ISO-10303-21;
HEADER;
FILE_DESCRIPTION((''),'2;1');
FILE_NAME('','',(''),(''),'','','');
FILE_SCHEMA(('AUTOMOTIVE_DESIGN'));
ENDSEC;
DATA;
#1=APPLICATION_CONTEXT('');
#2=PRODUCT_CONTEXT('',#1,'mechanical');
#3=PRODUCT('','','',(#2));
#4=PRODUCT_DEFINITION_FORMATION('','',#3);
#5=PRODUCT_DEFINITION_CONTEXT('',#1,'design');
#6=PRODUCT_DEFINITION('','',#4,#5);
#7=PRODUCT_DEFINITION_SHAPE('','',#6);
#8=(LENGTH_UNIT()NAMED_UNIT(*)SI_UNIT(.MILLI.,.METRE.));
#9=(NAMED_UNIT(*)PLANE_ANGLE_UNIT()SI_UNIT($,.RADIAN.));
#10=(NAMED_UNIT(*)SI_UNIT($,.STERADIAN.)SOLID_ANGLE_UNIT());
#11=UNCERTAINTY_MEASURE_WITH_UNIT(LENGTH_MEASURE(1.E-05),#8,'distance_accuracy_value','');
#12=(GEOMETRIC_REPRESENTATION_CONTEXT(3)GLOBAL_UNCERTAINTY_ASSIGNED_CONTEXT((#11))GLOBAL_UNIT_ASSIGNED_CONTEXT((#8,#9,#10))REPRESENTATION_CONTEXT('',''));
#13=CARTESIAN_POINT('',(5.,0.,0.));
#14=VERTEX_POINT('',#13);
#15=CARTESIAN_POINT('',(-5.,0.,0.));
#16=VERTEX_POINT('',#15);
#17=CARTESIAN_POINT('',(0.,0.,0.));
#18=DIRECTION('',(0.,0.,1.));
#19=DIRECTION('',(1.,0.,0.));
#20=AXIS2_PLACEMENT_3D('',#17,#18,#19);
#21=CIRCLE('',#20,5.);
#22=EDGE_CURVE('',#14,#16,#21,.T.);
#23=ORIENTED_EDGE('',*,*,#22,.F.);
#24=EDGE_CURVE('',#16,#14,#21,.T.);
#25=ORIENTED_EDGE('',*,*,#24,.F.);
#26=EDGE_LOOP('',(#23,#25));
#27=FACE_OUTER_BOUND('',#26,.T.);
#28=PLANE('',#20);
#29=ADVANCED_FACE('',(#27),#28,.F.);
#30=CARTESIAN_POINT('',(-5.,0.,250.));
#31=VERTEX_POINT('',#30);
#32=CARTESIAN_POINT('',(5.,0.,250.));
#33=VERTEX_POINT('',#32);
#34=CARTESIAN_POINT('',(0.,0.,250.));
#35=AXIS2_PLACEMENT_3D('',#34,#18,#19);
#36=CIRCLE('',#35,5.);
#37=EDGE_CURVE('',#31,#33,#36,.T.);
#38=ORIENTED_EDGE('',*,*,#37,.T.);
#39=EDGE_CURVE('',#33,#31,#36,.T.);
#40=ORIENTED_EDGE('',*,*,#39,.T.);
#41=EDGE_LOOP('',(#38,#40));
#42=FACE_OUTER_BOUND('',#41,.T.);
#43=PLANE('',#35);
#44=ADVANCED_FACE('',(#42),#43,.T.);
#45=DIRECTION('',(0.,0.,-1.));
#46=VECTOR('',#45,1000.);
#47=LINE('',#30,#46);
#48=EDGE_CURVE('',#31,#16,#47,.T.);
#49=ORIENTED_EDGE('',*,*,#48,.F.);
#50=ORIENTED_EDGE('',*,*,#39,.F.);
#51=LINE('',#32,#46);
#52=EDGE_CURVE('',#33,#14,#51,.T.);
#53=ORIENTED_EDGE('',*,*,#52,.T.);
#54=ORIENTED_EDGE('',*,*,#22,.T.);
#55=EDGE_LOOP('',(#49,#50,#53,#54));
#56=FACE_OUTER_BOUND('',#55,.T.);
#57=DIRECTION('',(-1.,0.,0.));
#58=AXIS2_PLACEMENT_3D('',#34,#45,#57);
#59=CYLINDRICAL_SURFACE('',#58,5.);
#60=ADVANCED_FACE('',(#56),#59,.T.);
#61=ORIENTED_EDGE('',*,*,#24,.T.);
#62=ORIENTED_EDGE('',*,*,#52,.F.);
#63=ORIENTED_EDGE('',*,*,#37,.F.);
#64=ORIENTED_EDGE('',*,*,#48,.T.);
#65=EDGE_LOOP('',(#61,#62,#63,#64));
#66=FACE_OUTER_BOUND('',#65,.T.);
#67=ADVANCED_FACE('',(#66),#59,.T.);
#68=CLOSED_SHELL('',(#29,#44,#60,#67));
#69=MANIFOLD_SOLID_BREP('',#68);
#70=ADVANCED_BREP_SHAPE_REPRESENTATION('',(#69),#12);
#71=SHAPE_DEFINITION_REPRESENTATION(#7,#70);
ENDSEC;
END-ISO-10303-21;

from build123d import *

# Parameters (mm, degrees)
SKETCH1_R           = 5
BOSS_EXTRUDE1_DEPTH = 250


with BuildPart() as part:
    # Sketch1 → Boss-Extrude1 (new body)
    with BuildSketch(Plane.XY):
        Circle(SKETCH1_R)
    extrude(amount=BOSS_EXTRUDE1_DEPTH)


solid = part.part
